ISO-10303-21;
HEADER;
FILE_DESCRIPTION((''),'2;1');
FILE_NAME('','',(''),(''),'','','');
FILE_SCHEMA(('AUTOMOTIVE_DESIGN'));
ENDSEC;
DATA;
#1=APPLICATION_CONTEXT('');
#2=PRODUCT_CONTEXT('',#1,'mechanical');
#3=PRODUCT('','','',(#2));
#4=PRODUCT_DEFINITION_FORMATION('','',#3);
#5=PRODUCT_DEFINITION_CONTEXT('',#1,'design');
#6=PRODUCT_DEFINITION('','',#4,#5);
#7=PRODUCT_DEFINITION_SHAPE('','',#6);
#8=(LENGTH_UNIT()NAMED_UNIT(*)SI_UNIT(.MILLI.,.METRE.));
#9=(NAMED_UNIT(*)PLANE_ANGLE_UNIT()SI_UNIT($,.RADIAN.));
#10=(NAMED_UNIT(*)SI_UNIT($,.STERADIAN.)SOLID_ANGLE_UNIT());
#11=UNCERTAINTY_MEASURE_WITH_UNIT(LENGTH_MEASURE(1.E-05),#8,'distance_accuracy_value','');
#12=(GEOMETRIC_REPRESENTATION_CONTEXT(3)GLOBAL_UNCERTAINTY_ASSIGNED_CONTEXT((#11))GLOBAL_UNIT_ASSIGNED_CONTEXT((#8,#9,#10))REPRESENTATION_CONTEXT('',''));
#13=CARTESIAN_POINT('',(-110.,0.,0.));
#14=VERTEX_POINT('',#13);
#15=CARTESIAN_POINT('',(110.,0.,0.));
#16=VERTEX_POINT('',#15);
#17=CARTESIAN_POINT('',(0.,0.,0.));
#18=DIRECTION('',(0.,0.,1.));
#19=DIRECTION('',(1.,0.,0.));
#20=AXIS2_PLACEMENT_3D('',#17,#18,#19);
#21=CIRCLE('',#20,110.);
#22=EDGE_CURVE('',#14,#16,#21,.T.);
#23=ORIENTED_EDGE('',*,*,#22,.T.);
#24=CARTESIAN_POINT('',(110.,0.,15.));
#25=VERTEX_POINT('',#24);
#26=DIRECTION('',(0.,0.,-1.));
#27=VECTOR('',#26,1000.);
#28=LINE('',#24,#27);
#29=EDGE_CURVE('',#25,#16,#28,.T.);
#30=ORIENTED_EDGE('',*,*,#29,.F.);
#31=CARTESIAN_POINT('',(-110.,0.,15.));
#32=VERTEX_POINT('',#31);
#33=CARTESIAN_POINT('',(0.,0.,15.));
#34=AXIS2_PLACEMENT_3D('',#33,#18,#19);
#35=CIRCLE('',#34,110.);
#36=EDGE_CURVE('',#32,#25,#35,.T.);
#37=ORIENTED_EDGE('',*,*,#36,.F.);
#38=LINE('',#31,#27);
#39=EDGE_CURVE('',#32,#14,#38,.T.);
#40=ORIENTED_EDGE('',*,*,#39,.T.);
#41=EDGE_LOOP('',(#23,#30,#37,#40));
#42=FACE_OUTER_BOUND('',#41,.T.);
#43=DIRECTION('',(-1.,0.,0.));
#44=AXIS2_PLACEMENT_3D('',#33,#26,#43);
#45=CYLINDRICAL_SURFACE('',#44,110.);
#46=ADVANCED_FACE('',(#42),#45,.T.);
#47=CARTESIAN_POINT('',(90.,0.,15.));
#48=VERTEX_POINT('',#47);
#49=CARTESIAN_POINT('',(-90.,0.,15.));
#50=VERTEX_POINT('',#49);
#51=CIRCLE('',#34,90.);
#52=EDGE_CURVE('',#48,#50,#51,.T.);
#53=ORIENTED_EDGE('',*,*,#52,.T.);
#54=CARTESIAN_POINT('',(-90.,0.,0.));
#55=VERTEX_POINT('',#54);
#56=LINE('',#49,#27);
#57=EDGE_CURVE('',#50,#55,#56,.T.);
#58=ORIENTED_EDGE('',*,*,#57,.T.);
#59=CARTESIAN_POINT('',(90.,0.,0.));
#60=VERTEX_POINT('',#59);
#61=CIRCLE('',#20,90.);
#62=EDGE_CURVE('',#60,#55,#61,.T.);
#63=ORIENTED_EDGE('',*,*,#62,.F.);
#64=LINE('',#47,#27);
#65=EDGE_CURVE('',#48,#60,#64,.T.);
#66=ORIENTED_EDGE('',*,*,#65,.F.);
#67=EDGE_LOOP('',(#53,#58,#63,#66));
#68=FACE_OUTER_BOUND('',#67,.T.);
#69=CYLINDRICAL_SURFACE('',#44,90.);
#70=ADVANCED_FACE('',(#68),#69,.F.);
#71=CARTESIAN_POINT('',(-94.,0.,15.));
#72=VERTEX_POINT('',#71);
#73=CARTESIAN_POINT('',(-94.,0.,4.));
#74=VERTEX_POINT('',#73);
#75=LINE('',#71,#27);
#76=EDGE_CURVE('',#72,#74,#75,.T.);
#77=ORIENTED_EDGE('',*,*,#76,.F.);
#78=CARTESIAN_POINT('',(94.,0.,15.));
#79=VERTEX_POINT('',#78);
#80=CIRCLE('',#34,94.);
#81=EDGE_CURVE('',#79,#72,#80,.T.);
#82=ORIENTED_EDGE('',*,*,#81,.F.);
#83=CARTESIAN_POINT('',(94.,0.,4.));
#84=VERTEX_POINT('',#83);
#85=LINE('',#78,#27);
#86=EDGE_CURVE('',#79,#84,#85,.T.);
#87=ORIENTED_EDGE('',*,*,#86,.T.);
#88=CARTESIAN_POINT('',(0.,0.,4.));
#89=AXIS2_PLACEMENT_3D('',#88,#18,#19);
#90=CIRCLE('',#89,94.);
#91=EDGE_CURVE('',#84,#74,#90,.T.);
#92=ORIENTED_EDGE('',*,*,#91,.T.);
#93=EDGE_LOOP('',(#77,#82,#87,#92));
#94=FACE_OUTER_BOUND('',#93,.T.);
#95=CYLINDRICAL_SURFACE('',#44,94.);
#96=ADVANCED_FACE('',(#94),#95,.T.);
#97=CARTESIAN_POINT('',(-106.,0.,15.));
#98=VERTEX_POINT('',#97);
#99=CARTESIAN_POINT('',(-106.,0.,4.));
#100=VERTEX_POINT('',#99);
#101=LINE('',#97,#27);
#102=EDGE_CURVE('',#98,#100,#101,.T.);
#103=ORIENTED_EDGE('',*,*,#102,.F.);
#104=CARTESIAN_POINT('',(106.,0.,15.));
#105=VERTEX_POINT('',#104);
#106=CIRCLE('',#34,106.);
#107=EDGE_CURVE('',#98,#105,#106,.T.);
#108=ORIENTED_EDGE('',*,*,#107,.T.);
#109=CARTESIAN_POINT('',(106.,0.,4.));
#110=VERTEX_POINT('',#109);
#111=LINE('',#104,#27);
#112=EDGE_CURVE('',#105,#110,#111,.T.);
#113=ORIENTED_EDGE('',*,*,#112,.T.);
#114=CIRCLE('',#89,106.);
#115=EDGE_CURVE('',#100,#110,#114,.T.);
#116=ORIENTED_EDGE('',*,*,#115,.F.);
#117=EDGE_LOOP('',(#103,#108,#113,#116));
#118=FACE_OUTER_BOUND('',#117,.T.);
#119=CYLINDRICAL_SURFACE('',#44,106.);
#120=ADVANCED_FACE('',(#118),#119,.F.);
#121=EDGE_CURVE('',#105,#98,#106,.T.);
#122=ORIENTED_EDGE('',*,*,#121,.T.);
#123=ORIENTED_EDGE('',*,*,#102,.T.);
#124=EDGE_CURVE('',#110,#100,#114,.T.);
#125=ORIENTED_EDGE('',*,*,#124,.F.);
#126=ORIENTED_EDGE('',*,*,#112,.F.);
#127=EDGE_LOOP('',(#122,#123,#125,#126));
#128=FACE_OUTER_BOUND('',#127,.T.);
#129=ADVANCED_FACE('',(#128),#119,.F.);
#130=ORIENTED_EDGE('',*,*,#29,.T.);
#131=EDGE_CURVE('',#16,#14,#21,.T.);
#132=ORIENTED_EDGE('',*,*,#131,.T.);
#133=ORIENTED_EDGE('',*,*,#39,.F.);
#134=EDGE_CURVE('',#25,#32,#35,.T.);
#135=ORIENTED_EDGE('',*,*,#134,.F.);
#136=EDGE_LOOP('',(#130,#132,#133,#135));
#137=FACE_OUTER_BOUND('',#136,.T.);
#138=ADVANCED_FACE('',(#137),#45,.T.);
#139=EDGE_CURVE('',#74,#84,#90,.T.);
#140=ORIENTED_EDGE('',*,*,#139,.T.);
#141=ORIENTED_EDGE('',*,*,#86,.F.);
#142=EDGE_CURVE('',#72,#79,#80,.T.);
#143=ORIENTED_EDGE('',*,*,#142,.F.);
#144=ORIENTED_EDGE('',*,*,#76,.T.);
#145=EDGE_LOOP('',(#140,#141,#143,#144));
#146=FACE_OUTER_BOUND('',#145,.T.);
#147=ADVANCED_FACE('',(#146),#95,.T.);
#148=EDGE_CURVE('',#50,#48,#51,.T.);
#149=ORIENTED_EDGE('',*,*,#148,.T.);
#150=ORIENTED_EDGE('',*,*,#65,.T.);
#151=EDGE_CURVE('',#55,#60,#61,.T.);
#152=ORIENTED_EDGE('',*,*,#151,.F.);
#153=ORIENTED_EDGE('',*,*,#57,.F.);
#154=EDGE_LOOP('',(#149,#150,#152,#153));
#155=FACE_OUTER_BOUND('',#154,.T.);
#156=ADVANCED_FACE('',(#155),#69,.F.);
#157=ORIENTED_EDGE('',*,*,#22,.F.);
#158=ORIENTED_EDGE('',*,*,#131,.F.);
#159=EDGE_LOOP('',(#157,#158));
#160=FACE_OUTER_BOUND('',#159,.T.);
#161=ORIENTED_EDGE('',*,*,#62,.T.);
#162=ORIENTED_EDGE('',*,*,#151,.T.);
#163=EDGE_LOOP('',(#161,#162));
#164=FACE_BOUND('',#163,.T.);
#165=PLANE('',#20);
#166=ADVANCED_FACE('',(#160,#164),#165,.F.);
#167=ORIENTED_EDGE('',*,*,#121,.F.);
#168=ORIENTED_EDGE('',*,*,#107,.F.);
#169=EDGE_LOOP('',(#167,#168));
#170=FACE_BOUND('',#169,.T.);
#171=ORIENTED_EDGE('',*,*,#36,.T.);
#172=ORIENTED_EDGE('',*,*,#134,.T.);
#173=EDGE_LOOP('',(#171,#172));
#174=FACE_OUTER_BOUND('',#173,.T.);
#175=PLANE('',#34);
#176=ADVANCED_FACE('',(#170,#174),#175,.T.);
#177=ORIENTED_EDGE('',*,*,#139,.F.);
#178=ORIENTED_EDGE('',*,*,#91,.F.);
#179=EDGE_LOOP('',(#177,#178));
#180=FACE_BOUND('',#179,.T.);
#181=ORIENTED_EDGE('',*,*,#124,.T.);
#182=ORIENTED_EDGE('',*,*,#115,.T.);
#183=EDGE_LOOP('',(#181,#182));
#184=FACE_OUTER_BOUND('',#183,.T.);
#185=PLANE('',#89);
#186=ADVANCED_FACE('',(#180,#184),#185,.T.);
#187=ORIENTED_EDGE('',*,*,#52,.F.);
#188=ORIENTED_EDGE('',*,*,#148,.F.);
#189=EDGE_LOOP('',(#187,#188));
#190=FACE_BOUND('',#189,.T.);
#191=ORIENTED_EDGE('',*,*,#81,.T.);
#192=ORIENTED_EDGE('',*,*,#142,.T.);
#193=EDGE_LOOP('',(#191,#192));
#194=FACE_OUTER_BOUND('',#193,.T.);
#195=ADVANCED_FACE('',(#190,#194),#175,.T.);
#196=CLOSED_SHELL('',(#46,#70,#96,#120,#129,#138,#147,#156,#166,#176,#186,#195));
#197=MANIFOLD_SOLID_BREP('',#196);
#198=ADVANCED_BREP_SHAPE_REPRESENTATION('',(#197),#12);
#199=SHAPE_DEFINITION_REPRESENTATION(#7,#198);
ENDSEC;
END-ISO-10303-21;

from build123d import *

# Parameters (mm, degrees)
SKETCH1_R           = 110
SKETCH1_R_2         = 90
BOSS_EXTRUDE1_DEPTH = 15
SHELL1_T            = -4


with BuildPart() as part:
    # Sketch1 → Boss-Extrude1 (new body)
    with BuildSketch(Plane.XY):
        Circle(SKETCH1_R)
        Circle(SKETCH1_R_2, mode=Mode.SUBTRACT)
    extrude(amount=BOSS_EXTRUDE1_DEPTH)

    # Shell1
    shell1_openings = [part.faces().sort_by_distance(p)[0] for p in [
        (-106.888730163, 0, 15),
    ]]
    offset(amount=SHELL1_T, openings=shell1_openings, kind=Kind.INTERSECTION)


solid = part.part
